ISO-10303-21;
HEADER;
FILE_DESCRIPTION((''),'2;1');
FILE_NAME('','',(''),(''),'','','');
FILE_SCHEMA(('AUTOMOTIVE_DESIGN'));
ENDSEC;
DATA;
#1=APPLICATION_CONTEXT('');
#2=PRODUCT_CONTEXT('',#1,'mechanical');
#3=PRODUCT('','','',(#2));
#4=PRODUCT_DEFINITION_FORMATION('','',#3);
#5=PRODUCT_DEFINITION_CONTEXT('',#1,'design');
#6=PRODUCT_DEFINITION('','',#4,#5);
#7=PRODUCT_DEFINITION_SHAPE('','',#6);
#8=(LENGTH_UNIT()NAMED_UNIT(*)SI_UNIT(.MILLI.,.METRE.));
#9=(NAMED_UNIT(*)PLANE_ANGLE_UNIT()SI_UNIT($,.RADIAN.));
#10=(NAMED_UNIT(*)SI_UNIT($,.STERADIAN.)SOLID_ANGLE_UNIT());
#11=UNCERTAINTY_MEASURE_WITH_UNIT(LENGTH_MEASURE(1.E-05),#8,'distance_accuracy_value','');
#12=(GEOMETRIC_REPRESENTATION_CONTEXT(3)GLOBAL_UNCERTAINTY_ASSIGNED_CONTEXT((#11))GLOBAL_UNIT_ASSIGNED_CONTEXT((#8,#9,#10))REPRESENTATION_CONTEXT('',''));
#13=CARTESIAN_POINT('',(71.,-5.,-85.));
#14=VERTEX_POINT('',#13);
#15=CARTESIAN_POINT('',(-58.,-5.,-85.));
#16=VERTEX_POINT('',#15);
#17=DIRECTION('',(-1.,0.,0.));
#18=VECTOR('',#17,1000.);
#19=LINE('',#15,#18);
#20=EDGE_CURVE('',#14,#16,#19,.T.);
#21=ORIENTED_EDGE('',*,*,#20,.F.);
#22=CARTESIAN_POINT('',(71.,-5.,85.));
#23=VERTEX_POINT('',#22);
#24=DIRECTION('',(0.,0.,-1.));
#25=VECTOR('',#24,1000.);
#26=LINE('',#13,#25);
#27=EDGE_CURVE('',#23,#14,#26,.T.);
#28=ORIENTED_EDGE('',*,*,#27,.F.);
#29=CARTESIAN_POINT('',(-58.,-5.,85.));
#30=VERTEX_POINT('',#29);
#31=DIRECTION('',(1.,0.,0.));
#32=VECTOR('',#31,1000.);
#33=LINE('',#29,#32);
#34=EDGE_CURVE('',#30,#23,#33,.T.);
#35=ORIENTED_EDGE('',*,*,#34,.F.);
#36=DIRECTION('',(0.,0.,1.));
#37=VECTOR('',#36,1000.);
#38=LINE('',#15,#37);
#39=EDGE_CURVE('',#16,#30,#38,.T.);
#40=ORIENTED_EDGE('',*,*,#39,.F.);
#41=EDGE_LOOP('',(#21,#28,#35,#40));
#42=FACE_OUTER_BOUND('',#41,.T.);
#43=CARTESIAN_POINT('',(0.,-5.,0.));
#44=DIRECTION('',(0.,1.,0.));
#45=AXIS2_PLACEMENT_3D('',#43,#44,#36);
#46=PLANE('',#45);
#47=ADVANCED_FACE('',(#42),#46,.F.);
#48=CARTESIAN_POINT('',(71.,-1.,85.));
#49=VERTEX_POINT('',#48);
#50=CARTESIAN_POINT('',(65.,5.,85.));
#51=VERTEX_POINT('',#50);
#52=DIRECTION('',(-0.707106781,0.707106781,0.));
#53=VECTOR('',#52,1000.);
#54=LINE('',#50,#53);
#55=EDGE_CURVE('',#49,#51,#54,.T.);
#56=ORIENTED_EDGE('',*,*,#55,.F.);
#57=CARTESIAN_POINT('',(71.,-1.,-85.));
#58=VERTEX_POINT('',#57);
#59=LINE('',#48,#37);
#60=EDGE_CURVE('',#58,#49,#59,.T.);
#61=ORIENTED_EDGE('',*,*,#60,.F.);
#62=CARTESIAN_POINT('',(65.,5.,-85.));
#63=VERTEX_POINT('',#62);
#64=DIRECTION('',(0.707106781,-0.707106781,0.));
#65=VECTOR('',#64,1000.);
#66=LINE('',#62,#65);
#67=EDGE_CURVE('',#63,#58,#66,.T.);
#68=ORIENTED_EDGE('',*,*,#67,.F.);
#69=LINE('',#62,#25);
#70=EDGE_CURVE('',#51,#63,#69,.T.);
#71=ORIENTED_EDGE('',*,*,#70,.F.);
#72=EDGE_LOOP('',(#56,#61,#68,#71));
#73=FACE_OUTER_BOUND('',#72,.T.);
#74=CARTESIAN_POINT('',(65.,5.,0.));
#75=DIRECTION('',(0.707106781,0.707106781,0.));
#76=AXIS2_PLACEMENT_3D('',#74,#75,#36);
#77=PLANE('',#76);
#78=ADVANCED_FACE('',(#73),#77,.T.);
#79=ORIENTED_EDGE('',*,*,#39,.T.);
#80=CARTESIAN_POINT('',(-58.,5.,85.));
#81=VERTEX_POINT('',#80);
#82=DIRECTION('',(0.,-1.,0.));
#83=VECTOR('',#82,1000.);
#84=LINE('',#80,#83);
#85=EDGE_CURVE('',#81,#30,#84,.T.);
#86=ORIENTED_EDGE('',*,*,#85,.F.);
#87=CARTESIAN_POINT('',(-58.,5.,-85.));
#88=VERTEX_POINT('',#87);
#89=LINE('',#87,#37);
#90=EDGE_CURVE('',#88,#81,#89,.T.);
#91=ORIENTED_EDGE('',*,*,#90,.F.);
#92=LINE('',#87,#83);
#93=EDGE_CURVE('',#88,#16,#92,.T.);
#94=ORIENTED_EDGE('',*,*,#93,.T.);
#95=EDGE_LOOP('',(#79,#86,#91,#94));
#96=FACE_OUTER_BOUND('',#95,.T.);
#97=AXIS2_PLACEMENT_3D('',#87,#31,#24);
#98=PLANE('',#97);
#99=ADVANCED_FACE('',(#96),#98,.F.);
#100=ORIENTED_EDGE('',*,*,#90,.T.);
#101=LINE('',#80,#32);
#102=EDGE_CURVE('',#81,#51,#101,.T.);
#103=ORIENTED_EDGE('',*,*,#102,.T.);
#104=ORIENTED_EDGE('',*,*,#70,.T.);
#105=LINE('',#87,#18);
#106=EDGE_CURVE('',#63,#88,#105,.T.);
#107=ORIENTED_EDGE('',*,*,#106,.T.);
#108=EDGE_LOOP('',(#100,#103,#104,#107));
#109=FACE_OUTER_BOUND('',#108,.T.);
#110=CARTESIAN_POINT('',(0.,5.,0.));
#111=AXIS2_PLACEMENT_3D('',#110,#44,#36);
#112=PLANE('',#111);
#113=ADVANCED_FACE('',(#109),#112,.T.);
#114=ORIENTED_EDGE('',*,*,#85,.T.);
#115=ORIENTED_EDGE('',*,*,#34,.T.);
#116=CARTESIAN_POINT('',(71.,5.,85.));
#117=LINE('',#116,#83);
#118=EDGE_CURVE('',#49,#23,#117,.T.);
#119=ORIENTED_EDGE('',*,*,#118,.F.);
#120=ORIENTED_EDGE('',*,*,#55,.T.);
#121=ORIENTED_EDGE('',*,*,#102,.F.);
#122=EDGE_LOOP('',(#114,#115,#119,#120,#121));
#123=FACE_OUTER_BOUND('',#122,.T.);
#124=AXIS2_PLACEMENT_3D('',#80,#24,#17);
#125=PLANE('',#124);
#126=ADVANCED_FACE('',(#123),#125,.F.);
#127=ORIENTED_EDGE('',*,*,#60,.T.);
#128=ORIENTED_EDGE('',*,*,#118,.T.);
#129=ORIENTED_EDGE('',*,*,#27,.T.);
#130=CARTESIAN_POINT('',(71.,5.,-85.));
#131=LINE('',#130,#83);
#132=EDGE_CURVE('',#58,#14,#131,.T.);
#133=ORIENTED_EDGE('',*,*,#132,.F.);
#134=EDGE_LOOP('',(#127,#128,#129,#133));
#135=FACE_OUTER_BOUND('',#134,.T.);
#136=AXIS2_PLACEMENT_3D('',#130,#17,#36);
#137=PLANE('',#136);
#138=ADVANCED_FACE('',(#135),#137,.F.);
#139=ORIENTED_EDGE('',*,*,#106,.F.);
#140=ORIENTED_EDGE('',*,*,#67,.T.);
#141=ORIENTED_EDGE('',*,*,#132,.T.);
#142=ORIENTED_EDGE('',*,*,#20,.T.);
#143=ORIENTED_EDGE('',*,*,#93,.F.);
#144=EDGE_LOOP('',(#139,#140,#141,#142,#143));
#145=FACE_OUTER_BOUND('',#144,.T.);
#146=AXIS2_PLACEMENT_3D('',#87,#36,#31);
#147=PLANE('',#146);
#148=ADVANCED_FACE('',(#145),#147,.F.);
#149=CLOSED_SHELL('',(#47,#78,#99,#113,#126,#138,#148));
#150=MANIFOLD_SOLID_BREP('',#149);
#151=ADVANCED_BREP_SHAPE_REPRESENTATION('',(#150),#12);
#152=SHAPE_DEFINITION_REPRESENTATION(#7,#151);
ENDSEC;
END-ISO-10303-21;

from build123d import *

# Parameters (mm, degrees)
SKETCH1_W           = 129
SKETCH1_H           = 170
BOSS_EXTRUDE1_DEPTH = 5
CHAMFER1_SIZE       = 6


with BuildPart() as part:
    # Sketch1 → Boss-Extrude1 (new, symmetric)
    with BuildSketch(Plane(origin=(0, 0, 0), x_dir=(1, 0, 0), z_dir=(0, 1, 0))):
        with Locations((6.5, 0)):
            Rectangle(SKETCH1_W, SKETCH1_H)
    extrude(amount=BOSS_EXTRUDE1_DEPTH, both=True)

    # Chamfer1
    chamfer1_edges = [part.edges().sort_by_distance(p)[0] for p in [
        (71, 5, 0),
    ]]
    chamfer(chamfer1_edges, length=CHAMFER1_SIZE)


solid = part.part
